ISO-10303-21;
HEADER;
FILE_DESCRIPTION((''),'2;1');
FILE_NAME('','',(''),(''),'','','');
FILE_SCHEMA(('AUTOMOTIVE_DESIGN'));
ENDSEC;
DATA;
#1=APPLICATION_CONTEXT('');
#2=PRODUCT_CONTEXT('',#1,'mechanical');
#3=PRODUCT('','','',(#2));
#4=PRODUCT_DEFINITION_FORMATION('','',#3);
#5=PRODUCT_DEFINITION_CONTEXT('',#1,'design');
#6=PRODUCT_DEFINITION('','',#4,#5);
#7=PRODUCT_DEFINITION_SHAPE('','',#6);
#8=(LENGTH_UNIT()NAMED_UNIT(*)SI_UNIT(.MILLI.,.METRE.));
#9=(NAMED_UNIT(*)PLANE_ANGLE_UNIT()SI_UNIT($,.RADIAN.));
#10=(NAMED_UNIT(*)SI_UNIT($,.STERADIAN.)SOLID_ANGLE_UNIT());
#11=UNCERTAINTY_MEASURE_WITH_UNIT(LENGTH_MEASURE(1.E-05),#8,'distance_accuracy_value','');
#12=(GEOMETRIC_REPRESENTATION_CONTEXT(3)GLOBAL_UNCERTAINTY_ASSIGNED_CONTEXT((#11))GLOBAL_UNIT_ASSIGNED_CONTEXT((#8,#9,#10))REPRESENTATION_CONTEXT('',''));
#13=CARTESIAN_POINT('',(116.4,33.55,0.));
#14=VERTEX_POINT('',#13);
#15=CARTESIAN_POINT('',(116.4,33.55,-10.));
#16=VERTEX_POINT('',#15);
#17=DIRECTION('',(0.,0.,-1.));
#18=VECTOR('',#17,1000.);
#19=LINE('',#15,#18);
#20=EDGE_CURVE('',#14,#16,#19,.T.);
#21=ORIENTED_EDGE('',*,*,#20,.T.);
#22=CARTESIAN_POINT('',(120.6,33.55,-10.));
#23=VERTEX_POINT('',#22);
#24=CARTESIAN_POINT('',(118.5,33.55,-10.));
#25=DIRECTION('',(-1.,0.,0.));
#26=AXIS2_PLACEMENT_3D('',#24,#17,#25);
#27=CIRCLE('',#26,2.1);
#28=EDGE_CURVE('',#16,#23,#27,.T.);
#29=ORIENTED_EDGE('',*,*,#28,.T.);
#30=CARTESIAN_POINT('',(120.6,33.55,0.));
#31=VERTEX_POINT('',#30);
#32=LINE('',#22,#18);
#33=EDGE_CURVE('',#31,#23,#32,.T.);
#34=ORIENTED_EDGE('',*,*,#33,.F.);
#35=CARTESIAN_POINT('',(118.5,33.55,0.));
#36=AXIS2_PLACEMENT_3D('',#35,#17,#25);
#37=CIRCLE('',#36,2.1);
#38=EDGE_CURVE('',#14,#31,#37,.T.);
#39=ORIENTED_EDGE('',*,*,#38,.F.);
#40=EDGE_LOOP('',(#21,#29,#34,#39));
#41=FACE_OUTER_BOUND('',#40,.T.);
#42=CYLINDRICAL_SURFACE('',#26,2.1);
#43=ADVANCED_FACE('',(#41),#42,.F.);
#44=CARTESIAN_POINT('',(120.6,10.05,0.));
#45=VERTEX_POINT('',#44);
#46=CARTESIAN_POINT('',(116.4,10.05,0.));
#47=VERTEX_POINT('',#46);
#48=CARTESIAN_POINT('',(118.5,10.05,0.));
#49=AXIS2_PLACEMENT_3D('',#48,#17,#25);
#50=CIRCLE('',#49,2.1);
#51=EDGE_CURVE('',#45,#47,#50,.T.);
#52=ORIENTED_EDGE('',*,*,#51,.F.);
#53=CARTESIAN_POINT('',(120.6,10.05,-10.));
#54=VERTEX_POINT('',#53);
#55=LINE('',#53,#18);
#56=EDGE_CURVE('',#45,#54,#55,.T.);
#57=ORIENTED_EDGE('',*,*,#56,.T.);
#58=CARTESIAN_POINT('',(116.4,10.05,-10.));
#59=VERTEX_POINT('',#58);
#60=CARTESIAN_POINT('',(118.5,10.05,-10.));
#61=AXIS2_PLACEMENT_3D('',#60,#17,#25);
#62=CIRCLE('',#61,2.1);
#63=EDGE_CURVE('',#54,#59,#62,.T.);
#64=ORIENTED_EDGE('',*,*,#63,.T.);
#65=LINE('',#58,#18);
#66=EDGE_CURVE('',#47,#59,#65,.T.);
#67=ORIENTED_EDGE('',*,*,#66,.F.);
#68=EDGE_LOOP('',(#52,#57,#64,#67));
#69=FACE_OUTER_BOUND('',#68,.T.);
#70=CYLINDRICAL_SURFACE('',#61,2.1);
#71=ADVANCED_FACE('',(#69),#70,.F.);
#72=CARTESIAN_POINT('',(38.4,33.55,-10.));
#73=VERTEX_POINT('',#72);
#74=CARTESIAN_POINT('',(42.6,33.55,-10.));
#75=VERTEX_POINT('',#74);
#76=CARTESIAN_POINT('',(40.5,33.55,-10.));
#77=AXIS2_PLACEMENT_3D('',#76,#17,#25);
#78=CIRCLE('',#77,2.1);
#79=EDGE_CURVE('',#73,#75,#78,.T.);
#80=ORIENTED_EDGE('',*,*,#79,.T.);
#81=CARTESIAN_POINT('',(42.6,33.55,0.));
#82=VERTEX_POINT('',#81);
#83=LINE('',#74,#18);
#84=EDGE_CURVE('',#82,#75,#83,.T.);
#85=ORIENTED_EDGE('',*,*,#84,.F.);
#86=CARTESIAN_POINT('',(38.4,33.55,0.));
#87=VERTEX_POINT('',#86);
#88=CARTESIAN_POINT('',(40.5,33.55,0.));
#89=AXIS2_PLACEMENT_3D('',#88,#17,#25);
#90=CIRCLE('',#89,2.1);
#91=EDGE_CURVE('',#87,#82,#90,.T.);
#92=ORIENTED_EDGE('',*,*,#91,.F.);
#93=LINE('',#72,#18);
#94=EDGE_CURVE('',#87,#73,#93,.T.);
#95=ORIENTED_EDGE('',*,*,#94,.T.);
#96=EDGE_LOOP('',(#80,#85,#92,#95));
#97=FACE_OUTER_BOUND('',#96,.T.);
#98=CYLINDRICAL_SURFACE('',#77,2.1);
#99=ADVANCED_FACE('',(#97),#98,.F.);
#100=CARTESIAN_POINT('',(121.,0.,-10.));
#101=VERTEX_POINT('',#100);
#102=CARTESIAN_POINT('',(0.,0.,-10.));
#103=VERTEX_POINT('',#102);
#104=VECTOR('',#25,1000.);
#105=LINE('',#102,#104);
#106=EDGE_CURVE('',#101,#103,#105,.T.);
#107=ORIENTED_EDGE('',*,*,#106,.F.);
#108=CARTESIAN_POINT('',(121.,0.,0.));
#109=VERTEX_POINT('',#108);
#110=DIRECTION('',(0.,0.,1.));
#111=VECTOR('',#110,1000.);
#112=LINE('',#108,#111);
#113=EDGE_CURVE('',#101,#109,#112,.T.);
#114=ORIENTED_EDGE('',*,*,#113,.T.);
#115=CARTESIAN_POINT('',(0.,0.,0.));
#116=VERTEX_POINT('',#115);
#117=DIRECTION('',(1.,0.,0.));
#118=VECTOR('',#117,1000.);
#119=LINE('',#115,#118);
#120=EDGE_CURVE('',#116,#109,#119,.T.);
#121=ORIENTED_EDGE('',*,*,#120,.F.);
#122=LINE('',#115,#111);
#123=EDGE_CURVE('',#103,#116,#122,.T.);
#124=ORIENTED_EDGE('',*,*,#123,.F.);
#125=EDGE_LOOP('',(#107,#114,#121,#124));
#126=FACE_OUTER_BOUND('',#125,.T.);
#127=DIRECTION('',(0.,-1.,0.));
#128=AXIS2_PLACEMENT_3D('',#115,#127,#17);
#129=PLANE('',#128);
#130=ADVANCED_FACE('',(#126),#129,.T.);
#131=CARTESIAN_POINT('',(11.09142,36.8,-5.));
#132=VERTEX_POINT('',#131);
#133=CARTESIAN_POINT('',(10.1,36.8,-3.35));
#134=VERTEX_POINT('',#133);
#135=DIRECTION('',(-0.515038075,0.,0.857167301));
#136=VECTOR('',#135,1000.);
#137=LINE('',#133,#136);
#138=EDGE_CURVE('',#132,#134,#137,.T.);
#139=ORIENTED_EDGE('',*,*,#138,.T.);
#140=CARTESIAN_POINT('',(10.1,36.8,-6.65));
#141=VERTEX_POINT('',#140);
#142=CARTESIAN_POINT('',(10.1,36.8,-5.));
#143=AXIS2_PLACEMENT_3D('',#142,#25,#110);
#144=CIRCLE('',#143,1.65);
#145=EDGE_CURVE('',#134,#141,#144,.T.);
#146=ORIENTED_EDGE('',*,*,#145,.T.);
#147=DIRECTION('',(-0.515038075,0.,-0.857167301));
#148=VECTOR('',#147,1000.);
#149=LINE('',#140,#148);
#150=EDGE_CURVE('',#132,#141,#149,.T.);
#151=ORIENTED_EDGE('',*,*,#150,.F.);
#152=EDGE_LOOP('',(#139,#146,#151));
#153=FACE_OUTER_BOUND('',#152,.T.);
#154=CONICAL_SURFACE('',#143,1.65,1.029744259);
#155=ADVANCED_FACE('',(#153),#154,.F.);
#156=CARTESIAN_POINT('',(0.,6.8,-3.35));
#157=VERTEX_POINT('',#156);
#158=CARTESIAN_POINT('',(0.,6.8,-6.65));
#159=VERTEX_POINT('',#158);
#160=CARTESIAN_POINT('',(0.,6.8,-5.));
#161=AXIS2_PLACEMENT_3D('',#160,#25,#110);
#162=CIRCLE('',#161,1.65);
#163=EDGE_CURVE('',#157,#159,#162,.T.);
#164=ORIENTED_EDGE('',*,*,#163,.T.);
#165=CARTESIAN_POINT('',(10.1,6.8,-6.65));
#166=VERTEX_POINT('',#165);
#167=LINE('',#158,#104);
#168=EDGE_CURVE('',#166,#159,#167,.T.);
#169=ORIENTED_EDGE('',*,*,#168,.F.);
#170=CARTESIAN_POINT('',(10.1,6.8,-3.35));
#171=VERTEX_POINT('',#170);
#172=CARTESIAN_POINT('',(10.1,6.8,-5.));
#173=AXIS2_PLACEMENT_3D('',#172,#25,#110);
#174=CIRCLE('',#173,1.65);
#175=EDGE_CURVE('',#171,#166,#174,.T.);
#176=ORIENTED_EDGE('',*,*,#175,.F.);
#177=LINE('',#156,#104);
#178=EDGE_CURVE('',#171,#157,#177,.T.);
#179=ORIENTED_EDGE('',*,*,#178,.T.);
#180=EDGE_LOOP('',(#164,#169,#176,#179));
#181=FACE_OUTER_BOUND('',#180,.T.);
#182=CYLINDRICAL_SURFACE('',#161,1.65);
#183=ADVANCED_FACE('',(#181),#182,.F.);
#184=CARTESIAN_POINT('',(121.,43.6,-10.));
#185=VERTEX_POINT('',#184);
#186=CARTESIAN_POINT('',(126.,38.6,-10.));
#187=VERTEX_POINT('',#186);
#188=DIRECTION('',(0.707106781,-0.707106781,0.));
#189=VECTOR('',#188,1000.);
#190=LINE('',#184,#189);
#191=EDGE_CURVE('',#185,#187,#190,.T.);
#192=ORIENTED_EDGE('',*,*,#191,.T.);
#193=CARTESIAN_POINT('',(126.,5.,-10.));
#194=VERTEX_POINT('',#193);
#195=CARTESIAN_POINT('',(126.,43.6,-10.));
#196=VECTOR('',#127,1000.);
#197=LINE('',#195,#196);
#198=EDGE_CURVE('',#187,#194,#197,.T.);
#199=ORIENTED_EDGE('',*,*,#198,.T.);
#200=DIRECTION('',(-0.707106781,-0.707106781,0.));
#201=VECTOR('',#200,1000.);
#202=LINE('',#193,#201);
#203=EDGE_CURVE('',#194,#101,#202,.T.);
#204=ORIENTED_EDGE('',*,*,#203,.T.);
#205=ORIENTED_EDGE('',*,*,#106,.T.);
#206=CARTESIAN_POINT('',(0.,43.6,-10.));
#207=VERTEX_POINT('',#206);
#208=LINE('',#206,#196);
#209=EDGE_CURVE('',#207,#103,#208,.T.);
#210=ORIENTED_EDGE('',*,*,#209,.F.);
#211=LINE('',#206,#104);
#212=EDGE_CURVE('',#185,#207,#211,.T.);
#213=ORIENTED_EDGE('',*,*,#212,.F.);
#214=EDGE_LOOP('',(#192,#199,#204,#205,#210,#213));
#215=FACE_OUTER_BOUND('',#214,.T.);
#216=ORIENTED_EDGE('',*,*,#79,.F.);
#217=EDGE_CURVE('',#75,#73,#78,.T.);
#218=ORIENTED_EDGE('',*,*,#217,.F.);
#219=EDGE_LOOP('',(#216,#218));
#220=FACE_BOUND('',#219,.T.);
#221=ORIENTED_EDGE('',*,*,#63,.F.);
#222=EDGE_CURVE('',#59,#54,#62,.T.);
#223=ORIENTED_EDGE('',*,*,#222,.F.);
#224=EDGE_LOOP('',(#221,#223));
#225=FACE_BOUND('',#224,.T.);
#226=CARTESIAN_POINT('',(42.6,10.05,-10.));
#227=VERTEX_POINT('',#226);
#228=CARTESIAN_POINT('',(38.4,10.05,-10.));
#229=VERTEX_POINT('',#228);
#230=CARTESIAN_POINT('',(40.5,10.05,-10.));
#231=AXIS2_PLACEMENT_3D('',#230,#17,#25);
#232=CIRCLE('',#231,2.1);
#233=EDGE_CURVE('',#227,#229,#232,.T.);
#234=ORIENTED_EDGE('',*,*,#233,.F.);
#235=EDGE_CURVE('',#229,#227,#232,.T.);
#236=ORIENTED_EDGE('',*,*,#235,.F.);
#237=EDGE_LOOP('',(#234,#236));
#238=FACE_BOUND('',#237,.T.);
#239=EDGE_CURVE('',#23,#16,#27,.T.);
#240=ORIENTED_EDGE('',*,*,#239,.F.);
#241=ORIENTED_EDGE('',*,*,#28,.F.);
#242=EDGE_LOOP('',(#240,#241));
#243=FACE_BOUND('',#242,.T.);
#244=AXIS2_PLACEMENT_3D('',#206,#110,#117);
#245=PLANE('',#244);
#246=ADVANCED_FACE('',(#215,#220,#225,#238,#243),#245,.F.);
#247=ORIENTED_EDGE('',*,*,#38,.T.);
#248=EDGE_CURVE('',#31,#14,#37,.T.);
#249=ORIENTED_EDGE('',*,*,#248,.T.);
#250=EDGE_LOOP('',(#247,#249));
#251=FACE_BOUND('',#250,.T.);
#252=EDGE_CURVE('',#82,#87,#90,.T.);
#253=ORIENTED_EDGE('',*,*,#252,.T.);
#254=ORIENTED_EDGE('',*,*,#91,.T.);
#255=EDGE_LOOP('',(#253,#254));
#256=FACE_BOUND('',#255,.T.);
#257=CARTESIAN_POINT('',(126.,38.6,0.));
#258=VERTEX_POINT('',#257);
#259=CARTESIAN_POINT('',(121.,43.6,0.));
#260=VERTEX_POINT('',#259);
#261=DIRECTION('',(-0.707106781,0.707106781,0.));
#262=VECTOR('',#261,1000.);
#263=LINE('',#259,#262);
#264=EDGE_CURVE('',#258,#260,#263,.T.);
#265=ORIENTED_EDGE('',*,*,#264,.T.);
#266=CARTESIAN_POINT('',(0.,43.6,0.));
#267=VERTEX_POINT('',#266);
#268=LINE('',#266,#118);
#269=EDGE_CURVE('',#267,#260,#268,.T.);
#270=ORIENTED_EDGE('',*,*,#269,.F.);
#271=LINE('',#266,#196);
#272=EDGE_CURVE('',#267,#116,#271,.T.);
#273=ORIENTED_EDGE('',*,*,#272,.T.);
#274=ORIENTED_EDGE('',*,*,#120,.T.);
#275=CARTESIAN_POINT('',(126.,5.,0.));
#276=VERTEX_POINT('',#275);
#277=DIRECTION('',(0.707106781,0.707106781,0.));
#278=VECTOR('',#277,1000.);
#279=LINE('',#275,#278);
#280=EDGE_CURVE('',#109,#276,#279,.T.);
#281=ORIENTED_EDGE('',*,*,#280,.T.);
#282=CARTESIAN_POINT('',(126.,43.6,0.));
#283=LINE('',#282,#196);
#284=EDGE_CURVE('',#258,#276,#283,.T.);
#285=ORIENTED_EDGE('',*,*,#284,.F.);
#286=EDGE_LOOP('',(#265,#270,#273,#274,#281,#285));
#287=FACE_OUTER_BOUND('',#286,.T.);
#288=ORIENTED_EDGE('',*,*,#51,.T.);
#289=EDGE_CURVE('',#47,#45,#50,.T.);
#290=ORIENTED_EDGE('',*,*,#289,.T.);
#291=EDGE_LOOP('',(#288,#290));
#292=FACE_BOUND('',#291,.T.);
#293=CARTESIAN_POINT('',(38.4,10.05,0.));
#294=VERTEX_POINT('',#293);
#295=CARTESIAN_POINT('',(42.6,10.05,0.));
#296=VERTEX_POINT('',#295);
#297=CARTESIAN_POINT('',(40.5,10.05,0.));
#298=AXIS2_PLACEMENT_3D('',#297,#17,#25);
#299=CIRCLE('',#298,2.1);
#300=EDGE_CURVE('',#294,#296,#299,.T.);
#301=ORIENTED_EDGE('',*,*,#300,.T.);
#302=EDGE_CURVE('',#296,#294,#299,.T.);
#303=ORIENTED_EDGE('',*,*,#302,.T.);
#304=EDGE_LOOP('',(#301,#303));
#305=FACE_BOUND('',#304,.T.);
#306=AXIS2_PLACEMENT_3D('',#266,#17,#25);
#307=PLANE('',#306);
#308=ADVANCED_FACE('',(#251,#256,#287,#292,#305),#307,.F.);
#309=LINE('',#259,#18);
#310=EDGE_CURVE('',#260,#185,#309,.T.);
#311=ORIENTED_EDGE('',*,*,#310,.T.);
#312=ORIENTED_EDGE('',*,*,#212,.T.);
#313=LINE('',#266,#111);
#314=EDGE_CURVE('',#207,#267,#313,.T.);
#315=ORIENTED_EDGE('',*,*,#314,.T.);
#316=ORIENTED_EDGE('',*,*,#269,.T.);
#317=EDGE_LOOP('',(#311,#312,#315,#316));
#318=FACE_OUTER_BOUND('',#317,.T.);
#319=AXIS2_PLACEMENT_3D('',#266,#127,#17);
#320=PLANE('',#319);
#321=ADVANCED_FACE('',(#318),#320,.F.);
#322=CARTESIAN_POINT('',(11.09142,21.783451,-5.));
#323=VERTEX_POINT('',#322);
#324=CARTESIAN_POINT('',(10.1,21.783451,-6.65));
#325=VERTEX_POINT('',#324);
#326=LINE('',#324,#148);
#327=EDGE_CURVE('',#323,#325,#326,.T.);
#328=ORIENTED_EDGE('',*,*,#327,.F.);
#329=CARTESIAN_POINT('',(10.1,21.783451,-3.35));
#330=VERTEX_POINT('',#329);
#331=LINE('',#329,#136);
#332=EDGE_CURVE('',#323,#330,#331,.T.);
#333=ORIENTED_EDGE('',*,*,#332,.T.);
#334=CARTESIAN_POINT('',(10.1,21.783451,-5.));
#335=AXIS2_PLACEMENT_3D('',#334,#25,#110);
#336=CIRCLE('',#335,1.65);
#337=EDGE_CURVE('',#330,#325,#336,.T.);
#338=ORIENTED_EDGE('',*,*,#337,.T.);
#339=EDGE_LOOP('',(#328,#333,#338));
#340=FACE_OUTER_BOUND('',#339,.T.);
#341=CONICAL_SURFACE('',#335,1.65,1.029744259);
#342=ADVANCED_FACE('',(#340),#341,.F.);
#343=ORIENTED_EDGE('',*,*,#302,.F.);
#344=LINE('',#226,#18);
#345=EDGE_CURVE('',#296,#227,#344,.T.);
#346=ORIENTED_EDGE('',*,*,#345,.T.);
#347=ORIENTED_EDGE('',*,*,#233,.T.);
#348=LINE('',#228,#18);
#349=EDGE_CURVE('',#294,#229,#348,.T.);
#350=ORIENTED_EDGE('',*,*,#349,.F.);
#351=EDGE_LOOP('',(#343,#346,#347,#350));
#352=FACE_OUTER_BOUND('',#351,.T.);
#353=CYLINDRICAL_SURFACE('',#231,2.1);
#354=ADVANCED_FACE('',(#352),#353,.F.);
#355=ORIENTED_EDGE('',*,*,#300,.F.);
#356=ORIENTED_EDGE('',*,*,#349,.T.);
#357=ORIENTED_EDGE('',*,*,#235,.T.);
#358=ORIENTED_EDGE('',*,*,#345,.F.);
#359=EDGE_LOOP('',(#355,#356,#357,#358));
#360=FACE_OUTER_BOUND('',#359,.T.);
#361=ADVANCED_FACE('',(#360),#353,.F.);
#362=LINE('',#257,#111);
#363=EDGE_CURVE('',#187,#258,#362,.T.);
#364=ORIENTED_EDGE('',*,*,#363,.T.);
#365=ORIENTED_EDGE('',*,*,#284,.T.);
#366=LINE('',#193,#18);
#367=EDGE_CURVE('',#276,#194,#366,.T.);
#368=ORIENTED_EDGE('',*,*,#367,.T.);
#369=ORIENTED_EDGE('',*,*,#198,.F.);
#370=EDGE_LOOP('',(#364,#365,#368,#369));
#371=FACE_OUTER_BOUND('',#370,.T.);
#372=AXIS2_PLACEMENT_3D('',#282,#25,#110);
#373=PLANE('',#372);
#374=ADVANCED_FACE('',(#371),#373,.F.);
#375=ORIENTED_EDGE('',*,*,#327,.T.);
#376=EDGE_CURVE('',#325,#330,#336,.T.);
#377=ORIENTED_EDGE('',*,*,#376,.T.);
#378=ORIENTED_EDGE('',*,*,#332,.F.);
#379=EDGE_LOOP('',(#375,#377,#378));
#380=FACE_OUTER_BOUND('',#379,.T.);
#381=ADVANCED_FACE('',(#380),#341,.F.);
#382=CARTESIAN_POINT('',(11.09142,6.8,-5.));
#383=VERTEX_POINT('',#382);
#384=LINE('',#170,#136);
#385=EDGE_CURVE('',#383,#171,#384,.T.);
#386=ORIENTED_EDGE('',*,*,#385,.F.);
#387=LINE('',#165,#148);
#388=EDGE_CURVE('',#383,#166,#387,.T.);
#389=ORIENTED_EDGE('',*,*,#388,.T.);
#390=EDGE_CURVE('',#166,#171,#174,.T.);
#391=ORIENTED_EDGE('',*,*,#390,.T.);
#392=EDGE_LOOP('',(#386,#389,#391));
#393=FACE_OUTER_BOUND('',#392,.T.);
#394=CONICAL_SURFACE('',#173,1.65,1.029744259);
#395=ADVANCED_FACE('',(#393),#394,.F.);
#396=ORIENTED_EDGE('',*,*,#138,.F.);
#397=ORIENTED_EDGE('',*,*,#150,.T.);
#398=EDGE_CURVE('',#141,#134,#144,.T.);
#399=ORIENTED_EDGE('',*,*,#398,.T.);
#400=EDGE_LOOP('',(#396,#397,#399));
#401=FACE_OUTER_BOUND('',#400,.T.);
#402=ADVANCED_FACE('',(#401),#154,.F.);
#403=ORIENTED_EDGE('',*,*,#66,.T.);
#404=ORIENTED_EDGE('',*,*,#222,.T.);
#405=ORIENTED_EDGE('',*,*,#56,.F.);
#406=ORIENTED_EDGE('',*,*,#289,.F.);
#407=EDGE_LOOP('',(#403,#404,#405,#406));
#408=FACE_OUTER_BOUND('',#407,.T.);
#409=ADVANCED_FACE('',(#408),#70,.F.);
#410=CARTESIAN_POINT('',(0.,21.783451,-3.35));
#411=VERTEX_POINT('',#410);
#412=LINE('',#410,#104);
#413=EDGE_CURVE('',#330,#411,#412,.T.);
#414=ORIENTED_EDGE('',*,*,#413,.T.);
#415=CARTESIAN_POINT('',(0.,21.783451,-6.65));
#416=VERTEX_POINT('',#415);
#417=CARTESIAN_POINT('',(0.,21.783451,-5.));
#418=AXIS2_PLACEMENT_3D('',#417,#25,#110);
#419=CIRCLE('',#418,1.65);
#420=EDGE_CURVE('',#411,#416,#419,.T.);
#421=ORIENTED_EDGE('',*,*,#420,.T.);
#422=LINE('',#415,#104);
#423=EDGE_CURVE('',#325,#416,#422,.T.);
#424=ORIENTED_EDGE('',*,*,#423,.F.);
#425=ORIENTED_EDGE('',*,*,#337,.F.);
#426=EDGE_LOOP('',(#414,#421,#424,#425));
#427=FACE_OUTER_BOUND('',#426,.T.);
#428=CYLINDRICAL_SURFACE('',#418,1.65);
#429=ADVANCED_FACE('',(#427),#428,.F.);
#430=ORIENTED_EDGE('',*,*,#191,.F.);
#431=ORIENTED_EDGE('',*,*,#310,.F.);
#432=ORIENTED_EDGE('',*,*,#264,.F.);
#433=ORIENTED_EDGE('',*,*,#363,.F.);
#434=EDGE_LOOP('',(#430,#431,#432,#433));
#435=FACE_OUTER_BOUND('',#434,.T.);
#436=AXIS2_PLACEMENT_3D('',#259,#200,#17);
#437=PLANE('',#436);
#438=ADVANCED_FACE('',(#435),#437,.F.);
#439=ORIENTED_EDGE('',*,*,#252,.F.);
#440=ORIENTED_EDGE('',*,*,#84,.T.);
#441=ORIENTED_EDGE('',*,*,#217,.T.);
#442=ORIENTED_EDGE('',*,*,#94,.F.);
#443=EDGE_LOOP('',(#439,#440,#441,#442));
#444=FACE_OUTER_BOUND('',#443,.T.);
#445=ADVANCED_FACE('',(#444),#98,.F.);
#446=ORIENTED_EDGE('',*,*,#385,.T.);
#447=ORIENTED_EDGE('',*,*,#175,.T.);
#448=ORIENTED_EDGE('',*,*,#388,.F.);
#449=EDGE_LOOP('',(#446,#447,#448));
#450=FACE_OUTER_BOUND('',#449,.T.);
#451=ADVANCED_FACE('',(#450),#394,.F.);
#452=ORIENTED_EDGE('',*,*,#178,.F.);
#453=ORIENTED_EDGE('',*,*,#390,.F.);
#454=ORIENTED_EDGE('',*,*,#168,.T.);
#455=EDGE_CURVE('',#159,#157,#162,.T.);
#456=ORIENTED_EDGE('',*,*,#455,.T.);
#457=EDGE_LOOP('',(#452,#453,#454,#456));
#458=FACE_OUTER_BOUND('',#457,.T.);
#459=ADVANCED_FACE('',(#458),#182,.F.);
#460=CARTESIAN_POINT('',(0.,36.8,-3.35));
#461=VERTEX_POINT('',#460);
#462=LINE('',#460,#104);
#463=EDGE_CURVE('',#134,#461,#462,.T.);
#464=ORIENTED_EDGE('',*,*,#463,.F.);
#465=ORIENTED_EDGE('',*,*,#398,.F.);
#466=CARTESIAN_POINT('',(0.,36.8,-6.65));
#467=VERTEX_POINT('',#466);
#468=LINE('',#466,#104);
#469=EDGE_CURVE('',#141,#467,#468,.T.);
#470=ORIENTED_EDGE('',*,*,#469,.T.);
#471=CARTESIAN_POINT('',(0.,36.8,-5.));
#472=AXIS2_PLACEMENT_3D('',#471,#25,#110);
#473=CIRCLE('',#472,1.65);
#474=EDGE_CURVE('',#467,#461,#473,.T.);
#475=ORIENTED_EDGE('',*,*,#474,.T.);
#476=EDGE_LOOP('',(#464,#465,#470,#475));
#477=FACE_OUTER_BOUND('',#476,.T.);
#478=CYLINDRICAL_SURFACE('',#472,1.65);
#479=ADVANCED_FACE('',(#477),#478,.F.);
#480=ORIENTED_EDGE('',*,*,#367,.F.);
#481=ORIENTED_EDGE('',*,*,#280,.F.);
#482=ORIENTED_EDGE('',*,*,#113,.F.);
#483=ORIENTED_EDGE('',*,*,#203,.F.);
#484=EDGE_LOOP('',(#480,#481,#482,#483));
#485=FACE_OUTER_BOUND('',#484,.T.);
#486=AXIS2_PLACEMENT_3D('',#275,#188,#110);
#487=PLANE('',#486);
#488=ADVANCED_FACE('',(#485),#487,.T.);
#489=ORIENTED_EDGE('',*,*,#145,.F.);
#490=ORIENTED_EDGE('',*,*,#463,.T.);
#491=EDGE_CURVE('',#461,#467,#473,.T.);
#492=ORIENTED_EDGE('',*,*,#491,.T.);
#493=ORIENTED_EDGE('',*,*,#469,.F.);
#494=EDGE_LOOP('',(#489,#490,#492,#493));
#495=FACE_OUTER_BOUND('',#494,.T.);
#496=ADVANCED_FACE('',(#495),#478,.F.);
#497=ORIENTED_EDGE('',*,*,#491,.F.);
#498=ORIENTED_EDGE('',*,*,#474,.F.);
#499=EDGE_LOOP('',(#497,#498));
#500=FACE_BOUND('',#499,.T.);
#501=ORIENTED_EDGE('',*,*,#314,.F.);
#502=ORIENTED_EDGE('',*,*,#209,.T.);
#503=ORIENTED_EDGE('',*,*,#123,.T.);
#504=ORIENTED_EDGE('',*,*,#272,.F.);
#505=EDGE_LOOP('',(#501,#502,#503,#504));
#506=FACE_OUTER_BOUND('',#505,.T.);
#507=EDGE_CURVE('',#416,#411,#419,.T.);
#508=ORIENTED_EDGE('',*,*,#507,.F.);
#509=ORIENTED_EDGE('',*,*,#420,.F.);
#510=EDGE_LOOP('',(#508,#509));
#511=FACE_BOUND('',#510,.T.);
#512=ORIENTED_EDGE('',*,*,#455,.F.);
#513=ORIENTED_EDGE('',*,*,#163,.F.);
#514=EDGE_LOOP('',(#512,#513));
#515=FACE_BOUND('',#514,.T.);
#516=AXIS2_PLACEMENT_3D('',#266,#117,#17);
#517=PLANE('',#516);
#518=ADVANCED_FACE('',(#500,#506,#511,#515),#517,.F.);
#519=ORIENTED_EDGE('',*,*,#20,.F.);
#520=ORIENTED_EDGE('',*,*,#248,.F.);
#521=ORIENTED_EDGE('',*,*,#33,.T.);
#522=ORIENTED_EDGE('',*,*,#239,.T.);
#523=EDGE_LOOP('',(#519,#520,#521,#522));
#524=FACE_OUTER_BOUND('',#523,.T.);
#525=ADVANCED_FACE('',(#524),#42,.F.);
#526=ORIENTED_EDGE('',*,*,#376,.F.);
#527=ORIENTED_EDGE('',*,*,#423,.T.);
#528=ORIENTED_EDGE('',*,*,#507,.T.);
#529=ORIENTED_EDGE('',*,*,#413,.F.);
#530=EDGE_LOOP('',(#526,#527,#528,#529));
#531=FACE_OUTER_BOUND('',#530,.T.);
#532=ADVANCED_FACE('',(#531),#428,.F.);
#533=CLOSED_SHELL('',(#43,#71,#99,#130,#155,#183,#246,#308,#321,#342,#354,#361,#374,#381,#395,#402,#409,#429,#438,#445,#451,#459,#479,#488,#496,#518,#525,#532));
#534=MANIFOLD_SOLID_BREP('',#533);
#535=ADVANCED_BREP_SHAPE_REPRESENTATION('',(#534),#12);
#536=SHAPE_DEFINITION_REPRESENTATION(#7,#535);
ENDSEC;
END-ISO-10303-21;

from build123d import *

# Parameters (mm, degrees)
SKETCH_1_W             = 126
SKETCH_1_H             = 10
EXTRUDE_1_DEPTH        = 43.6
CHAMFER_1_SIZE         = 5
HOLE_WIZARD_M4_1_D     = 3.3
HOLE_WIZARD_M4_1_DEPTH = 10.1
HOLE_WIZARD_M4_1_TIP   = 0.991420021
HOLE_WIZARD_M5_1_D     = 4.2


with BuildPart() as part:
    # 草图1 → 凸台-拉伸1 (new body)
    with BuildSketch(Plane(origin=(0, 0, 0), x_dir=(1, 0, 0), z_dir=(0, 1, 0))):
        with Locations((63, 5)):
            Rectangle(SKETCH_1_W, SKETCH_1_H)
    extrude(amount=EXTRUDE_1_DEPTH)

    # 倒角1
    chamfer_1_edges = [part.edges().sort_by_distance(p)[0] for p in [
        (126, 43.6, -5),
        (126, 0, -5),
    ]]
    chamfer(chamfer_1_edges, length=CHAMFER_1_SIZE)

    # M4 螺纹孔1
    with Locations(Plane.ZY):
        with Locations((-5, 36.8), (-5, 21.783451384), (-5, 6.8)):
            Hole(HOLE_WIZARD_M4_1_D / 2, depth=HOLE_WIZARD_M4_1_DEPTH)
            with Locations((0, 0, -(HOLE_WIZARD_M4_1_DEPTH + HOLE_WIZARD_M4_1_TIP / 2))):  # 118° drill point
                Cone(0, HOLE_WIZARD_M4_1_D / 2, HOLE_WIZARD_M4_1_TIP, mode=Mode.SUBTRACT)

    # M5 螺纹孔1 (through all)
    with Locations(Plane(origin=(0, 0, -10), x_dir=(-1, 0, 0), z_dir=(0, 0, -1))):
        with Locations((-40.5, 33.55), (-40.5, 10.05), (-118.5, 33.55), (-118.5, 10.05)):
            Hole(HOLE_WIZARD_M5_1_D / 2)


solid = part.part
